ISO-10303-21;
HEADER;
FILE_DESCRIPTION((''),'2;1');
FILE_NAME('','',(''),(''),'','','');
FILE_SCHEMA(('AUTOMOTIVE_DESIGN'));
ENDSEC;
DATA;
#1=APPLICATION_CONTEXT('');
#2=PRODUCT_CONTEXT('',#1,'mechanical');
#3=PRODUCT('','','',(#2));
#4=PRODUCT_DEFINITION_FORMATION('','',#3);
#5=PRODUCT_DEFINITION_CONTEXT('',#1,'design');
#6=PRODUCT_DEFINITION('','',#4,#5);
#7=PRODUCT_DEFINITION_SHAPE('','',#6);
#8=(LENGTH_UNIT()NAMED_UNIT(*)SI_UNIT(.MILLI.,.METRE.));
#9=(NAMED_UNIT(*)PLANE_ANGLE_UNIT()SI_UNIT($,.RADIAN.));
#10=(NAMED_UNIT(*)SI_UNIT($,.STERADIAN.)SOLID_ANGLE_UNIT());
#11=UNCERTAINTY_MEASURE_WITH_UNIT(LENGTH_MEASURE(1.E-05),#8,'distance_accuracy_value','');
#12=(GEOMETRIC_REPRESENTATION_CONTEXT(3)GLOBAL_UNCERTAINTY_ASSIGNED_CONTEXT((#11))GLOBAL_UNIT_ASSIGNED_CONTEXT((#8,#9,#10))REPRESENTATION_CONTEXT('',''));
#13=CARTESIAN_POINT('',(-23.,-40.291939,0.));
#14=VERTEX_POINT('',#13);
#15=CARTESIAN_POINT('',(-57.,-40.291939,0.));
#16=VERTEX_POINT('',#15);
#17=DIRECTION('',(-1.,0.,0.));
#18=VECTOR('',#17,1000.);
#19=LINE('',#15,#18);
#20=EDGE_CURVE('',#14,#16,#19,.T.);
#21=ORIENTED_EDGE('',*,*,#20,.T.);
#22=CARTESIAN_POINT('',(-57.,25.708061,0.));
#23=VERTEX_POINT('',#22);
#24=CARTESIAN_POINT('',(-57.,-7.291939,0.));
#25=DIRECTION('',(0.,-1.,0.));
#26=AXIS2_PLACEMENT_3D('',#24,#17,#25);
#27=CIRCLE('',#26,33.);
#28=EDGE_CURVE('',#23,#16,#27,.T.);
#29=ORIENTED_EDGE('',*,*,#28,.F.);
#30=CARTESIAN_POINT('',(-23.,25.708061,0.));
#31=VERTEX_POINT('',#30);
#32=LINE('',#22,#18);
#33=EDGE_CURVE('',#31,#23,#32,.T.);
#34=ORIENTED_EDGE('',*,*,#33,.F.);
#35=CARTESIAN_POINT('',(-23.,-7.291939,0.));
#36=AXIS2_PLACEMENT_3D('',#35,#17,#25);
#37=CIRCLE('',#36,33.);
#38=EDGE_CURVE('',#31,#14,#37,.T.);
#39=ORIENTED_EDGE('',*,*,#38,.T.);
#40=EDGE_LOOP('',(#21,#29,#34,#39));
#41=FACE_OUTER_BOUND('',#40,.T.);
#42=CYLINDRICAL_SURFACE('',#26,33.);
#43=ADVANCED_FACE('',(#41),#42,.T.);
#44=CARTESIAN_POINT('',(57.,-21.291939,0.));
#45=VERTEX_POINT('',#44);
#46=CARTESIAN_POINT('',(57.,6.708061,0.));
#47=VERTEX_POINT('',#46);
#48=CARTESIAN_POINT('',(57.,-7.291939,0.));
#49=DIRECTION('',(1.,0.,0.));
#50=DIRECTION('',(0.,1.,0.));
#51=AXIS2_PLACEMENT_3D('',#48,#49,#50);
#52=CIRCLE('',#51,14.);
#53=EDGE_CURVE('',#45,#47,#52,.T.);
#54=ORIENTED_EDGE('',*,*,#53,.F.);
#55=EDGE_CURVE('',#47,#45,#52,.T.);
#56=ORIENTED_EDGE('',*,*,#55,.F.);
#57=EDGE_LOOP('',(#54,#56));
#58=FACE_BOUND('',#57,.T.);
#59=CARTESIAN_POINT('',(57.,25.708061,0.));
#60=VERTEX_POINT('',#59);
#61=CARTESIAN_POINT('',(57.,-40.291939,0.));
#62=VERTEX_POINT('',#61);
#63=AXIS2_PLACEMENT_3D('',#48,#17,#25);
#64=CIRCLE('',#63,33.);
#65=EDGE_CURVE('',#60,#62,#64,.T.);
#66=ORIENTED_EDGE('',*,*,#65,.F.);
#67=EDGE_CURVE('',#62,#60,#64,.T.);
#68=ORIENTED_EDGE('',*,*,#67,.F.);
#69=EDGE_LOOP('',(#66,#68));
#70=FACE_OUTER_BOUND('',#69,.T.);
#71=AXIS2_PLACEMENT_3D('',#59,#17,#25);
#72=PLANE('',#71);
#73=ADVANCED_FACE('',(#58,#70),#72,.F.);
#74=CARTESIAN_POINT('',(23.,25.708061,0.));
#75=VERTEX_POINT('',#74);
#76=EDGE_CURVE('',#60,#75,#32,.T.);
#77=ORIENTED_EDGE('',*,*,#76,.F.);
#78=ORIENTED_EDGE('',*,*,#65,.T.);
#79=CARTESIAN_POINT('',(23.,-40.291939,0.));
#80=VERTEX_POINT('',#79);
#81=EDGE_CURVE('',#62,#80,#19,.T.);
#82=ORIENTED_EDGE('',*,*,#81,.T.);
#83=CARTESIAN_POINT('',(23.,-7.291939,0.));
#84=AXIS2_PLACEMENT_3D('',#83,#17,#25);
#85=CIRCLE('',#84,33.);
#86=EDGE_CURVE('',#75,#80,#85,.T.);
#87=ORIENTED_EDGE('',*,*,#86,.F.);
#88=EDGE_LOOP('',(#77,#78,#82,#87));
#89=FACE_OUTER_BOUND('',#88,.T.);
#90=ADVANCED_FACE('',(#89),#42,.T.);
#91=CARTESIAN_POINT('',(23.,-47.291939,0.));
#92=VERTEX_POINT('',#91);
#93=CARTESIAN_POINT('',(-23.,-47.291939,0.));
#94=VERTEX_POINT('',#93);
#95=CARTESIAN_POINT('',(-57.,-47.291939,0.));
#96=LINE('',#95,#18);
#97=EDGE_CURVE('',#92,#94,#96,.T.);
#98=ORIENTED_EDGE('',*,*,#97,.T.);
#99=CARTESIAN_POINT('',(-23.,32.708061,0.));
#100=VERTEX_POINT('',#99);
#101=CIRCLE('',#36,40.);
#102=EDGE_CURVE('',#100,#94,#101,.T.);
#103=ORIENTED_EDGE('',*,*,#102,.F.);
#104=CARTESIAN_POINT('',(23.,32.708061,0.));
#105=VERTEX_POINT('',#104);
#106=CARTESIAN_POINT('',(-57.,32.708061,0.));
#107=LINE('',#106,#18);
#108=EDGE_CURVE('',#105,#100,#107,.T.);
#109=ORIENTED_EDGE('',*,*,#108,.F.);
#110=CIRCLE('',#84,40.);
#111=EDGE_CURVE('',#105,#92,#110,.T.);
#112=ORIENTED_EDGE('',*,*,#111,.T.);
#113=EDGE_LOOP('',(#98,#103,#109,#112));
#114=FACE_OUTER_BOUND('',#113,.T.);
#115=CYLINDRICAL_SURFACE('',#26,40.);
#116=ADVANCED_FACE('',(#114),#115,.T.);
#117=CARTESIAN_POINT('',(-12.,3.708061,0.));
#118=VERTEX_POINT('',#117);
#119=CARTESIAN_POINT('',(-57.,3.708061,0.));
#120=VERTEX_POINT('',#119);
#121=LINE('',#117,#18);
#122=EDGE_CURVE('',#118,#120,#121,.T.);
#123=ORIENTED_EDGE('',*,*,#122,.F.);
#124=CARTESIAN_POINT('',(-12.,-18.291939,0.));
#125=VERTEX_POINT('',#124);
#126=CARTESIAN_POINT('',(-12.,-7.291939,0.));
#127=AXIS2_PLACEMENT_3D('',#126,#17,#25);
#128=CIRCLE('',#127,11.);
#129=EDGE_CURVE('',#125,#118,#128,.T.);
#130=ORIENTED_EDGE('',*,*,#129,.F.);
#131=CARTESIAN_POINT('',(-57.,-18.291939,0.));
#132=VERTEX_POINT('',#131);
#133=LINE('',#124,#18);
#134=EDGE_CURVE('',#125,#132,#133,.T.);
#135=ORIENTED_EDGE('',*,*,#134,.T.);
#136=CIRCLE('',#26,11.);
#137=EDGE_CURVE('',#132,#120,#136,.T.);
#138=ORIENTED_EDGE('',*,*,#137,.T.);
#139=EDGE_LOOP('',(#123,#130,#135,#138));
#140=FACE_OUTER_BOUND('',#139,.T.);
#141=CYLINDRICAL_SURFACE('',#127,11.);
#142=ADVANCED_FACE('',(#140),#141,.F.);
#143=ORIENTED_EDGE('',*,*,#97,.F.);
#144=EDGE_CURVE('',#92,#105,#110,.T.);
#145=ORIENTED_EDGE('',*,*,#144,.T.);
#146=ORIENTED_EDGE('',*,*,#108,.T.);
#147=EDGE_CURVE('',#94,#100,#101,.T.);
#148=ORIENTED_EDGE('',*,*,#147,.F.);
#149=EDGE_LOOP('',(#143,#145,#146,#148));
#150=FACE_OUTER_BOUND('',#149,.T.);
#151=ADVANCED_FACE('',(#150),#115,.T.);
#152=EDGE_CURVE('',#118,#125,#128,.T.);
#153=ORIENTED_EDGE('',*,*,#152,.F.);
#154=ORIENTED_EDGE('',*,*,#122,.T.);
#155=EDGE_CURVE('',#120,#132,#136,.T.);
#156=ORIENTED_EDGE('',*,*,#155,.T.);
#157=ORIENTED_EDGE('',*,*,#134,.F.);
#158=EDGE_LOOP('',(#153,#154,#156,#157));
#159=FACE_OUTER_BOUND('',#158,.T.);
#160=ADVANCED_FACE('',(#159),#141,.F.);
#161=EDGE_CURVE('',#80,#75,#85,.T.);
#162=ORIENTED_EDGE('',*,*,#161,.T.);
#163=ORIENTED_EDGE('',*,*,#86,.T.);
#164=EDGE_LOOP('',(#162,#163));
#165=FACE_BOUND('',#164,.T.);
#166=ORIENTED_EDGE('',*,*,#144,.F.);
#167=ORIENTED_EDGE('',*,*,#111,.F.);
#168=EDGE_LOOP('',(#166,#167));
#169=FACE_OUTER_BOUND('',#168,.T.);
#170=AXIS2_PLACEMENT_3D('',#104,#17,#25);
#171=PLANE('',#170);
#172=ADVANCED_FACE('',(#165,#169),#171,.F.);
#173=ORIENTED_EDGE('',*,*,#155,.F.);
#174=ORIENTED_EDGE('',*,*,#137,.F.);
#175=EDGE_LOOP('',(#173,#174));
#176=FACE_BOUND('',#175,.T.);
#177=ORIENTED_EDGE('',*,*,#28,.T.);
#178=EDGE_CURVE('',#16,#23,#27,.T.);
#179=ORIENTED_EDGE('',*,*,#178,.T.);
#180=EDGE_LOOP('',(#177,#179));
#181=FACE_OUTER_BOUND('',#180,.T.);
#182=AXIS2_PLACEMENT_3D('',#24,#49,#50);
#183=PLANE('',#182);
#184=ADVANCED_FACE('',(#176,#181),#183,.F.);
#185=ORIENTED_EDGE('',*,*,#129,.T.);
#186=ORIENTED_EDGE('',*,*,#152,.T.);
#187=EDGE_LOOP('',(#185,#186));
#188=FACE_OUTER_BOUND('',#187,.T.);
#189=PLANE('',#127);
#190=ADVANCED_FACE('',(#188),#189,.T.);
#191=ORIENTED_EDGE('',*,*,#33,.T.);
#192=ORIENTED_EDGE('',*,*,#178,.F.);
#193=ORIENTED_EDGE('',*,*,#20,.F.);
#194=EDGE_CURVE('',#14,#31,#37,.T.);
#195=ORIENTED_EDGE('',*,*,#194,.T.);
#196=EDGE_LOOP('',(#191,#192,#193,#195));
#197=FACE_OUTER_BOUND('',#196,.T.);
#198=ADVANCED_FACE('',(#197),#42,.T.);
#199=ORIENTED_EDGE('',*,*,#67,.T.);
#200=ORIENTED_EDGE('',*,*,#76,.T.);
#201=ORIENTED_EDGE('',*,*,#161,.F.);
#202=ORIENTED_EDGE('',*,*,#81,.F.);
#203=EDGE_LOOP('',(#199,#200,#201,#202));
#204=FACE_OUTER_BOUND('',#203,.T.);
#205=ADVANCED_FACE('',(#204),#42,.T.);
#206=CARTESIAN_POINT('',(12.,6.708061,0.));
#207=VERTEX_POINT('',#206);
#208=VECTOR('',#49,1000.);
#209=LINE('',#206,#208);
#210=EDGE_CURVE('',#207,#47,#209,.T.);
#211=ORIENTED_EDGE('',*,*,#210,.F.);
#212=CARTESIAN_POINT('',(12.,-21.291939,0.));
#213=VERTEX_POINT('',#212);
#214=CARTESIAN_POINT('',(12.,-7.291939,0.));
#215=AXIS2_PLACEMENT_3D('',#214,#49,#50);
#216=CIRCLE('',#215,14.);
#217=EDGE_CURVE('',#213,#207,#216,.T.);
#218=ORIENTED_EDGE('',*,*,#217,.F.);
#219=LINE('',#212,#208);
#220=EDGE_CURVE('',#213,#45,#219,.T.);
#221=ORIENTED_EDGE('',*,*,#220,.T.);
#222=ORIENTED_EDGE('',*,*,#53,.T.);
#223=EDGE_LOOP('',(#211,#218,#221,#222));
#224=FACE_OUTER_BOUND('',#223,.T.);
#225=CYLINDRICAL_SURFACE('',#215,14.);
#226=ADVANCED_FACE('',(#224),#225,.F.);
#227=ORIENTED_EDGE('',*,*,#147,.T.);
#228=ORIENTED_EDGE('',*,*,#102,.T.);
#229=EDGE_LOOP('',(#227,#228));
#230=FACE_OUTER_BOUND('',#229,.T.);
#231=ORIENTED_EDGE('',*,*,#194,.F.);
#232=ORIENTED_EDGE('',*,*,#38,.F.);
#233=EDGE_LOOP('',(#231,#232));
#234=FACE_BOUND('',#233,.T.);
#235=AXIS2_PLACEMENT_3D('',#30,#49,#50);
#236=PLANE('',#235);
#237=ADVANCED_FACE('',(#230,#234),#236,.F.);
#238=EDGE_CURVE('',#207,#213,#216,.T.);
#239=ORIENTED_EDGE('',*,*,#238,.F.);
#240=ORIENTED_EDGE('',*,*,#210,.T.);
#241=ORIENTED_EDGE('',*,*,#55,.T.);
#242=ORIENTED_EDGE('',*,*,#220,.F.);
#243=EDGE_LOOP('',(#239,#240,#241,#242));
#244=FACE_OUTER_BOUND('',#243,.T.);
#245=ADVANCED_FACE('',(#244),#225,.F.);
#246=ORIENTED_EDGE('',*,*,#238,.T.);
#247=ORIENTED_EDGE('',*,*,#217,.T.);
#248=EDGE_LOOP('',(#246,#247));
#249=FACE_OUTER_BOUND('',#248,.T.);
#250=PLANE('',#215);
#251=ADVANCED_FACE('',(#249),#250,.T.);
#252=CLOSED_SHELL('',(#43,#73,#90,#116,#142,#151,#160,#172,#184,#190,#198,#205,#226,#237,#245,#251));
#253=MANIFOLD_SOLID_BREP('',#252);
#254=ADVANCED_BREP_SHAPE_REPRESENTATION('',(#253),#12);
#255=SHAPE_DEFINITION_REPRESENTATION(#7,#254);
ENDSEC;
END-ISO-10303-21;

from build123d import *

# Parameters (mm, degrees)
SKETCH_2_R          = 11
CUT_EXTRUDE_1_DEPTH = 45
SKETCH_3_R          = 14
CUT_EXTRUDE_2_DEPTH = 45


with BuildPart() as part:
    # 草图1 → 旋转1 (revolve)
    with BuildSketch(Plane.XY, mode=Mode.PRIVATE) as revolve_1_sk:
        Polygon((-57, -7.291938998), (57, -7.291938998), (57, 25.708061002), (23, 25.708061002), (23, 32.708061002), (-23, 32.708061002), (-23, 25.708061002), (-57, 25.708061002), align=None)
    revolve(revolve_1_sk.sketch.rotate(Axis((-57, -7.291938998, 0), (1, 0, 0)), 180), axis=Axis((-57, -7.291938998, 0), (1, 0, 0)))

    # 草图2 → 切除-拉伸1 (cut)
    with BuildSketch(Plane.ZY.offset(57)):
        with Locations(Location((0, -7.291938998, 0), (0, 0, 270))):
            Circle(SKETCH_2_R)
    extrude(amount=-CUT_EXTRUDE_1_DEPTH, mode=Mode.SUBTRACT)

    # 草图3 → 切除-拉伸2 (cut)
    with BuildSketch(Plane(origin=(57, 0, 0), x_dir=(0, 0, -1), z_dir=(1, 0, 0))):
        with Locations(Location((0, -7.291938998, 0), (0, 0, 90))):
            Circle(SKETCH_3_R)
    extrude(amount=-CUT_EXTRUDE_2_DEPTH, mode=Mode.SUBTRACT)


solid = part.part
